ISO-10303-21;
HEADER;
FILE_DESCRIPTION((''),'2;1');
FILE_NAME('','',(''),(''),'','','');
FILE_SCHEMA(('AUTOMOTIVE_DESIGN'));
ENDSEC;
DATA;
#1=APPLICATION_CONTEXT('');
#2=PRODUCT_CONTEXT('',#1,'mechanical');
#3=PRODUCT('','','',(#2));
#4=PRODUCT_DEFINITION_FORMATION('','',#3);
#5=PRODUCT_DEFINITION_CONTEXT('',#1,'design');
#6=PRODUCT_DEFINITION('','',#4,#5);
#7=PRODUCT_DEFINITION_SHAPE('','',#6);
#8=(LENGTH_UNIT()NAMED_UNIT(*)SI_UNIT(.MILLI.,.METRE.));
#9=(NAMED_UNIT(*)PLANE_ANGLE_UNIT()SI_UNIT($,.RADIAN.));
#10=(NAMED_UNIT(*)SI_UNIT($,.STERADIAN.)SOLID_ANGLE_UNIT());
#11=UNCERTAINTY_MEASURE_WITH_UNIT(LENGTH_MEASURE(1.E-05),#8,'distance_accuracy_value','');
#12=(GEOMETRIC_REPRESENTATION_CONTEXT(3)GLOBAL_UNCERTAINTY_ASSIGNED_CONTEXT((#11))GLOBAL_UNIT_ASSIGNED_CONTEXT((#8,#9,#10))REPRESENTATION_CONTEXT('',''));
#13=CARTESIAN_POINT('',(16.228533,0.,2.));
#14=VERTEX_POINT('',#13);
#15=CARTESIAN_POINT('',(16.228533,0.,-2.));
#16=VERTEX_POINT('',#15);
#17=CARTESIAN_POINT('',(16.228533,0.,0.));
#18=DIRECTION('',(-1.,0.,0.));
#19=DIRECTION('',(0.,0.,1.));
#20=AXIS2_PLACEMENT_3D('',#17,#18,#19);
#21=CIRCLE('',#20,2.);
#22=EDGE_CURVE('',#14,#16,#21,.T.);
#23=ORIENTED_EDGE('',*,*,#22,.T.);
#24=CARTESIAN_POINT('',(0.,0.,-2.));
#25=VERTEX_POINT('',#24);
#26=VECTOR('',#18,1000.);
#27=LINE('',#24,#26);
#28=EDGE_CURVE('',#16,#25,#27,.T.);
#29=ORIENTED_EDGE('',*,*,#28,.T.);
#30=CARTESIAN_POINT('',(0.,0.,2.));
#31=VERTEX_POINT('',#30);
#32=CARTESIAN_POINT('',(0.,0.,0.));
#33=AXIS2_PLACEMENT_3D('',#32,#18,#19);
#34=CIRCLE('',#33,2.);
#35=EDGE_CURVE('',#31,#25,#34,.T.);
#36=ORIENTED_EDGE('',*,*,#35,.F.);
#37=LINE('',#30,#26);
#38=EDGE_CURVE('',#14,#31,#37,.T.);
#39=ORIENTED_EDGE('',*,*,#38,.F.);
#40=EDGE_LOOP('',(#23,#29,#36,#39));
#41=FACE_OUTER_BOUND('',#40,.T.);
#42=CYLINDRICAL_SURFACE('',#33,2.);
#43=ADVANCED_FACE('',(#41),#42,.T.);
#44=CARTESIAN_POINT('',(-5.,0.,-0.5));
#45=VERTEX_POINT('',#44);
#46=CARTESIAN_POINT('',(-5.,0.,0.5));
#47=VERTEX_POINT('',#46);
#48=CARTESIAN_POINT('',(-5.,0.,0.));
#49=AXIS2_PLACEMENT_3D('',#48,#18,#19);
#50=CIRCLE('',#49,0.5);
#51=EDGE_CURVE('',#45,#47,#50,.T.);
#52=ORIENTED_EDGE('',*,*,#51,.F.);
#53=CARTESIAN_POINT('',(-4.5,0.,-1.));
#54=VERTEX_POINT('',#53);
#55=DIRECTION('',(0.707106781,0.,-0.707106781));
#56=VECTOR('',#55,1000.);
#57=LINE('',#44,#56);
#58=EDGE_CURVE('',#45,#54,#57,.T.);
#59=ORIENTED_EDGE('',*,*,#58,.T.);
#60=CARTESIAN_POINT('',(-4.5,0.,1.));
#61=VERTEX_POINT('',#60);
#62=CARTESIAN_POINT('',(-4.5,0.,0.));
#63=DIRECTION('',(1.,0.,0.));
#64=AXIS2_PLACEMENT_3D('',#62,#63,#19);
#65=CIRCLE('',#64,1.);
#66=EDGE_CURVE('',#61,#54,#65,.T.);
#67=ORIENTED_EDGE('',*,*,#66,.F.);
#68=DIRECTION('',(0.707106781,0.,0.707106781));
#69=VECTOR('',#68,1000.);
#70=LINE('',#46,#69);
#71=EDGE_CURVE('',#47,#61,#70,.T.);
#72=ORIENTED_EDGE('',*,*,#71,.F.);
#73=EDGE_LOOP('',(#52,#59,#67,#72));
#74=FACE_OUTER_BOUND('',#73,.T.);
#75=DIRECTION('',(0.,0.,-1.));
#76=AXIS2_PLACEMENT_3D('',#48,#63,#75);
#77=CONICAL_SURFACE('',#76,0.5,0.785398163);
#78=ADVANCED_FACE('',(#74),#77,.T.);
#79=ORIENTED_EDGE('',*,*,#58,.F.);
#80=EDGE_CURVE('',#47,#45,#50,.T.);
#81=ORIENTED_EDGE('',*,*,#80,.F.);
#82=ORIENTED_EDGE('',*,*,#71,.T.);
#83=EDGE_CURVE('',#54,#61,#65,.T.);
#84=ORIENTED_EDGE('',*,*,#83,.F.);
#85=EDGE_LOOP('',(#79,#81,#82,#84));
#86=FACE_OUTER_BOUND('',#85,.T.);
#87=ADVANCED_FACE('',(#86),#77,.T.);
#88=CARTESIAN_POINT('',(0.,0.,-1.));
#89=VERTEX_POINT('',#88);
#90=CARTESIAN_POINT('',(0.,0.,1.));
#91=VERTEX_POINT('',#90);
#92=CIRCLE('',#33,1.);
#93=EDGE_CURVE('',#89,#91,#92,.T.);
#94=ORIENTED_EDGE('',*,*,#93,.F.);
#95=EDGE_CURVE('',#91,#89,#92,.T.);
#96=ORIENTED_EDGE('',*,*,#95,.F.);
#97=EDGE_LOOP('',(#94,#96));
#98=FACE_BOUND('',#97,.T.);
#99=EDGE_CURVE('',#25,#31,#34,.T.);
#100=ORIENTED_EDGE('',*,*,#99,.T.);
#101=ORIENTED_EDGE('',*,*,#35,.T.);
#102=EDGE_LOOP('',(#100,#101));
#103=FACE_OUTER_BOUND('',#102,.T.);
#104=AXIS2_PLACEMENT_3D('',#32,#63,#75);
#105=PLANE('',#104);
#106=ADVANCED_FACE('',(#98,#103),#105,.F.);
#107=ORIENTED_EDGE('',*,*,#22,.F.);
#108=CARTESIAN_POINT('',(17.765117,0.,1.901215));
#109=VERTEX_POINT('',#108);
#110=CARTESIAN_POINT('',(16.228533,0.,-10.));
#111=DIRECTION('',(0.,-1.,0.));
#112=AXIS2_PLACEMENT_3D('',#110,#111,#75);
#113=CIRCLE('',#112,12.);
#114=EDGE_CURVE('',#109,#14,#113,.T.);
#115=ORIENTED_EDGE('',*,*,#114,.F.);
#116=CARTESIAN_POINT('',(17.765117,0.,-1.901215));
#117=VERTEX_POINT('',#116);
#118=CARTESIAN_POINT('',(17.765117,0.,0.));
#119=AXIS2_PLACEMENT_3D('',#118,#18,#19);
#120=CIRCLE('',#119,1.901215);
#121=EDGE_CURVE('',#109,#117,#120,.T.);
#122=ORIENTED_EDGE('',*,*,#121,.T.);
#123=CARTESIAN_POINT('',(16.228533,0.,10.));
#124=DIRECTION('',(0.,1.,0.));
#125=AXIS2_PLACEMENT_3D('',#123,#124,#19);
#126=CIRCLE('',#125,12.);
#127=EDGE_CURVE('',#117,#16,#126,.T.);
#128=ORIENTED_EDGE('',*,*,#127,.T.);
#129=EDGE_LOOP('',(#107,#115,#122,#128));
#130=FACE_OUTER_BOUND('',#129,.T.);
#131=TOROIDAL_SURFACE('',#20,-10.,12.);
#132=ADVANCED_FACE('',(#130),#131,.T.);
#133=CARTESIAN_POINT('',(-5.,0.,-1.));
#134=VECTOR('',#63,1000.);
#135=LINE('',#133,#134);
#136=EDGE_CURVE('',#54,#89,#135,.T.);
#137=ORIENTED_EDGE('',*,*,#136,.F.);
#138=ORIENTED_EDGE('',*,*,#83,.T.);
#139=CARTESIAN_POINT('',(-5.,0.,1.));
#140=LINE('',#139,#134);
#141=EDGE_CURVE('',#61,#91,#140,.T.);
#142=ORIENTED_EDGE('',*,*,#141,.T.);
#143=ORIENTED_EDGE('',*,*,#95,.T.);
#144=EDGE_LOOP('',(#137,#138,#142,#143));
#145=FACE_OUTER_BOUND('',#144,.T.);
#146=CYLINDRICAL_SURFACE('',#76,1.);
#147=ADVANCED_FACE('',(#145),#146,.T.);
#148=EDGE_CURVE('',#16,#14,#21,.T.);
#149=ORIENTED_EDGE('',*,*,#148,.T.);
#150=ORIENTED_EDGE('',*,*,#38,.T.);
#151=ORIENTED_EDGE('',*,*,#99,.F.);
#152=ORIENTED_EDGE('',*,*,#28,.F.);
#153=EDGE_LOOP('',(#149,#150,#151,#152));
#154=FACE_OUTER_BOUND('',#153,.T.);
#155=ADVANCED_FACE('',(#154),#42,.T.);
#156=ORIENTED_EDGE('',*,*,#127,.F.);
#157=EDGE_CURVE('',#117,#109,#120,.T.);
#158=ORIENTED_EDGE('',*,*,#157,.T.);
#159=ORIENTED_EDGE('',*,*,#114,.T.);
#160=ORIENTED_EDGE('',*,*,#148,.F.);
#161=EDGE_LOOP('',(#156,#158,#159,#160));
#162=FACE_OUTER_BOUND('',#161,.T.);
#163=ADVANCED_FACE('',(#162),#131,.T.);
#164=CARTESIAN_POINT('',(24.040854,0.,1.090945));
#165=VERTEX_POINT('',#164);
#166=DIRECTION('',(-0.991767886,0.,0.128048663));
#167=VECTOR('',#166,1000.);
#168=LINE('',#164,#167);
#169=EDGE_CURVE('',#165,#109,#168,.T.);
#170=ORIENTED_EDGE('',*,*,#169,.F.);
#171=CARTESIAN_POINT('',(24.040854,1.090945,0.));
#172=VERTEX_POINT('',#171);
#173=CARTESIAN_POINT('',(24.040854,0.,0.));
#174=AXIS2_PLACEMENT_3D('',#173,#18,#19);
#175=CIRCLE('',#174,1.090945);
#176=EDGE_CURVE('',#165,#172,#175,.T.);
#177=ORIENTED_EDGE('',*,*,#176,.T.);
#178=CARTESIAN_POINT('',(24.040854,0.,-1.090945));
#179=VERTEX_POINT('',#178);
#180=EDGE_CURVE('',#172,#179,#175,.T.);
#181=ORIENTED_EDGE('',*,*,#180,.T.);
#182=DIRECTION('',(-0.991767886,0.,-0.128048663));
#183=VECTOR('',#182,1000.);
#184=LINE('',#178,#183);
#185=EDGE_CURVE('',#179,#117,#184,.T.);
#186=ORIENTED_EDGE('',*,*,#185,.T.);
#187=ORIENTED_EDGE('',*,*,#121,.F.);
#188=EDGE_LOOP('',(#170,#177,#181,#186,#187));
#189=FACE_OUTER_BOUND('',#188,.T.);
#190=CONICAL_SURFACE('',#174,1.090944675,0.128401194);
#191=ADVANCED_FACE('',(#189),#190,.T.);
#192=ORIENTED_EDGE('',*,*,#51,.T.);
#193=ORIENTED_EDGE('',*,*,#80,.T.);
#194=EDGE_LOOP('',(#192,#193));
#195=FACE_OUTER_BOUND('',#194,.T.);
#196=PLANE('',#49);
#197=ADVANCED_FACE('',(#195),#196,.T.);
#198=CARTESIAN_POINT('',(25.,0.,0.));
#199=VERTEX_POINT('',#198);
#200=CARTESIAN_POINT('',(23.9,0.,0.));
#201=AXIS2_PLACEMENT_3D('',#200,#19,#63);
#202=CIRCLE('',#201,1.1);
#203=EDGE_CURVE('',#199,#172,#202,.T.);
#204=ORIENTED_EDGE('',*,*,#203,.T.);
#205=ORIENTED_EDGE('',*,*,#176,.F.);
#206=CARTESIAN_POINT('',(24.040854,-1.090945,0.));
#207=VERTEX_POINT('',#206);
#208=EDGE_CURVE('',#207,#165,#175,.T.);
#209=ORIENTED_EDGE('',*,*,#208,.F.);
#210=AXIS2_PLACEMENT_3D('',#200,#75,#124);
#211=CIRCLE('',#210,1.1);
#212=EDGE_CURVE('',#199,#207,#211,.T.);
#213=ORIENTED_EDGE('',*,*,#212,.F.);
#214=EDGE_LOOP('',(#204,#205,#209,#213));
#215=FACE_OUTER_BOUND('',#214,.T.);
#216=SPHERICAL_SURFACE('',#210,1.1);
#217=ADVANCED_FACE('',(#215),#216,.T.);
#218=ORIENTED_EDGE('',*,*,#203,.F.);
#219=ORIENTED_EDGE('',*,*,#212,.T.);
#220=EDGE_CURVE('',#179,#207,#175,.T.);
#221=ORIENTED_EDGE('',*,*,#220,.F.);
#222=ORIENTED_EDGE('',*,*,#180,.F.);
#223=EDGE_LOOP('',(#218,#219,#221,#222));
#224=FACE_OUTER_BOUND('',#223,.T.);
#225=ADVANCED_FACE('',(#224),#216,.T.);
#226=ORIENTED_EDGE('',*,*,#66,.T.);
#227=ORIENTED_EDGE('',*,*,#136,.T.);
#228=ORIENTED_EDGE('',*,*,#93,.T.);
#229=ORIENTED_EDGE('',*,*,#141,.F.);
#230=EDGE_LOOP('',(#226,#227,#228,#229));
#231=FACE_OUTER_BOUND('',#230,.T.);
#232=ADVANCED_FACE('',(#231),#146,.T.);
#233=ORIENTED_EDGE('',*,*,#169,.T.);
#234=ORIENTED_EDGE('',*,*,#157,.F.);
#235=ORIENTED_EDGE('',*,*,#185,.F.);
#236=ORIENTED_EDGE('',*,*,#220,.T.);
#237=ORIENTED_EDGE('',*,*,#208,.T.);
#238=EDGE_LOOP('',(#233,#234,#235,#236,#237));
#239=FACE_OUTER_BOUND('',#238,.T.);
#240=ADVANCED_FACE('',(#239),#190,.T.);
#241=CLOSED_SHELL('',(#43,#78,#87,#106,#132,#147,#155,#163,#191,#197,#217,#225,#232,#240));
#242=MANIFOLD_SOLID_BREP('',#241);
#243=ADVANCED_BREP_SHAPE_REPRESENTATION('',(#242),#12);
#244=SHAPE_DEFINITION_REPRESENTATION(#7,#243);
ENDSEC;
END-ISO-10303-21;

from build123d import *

# Parameters (mm, degrees)
SKETCH2_R           = 1
BOSS_EXTRUDE1_DEPTH = 5
CHAMFER1_SIZE       = 0.5


with BuildPart() as part:
    # Sketch1 → Revolve1 (revolve)
    with BuildSketch(Plane.XY, mode=Mode.PRIVATE) as revolve1_sk:
        with BuildLine():
            Line((0, 0), (0, 2))
            Line((0, 2), (16.22853262, 2))
            ThreePointArc((16.22853262, 2), (16.998410661, 1.975278193), (17.765116572, 1.901214634))
            Line((17.765116572, 1.901214634), (24.040853529, 1.090944675))
            ThreePointArc((24.040853529, 1.090944675), (24.726117087, 0.72631299), (25, 0))
            Line((25, 0), (0, 0))
        make_face()
    revolve(revolve1_sk.sketch.rotate(Axis((0, 0, 0), (1, 0, 0)), 90), axis=Axis((0, 0, 0), (1, 0, 0)))

    # Sketch2 → Boss-Extrude1 (add)
    with BuildSketch(Plane.ZY):
        Circle(SKETCH2_R)
    extrude(amount=BOSS_EXTRUDE1_DEPTH)

    # Chamfer1
    chamfer1_edges = [part.edges().sort_by_distance(p)[0] for p in [
        (-5, 0, -1),
    ]]
    chamfer(chamfer1_edges, length=CHAMFER1_SIZE)


solid = part.part
